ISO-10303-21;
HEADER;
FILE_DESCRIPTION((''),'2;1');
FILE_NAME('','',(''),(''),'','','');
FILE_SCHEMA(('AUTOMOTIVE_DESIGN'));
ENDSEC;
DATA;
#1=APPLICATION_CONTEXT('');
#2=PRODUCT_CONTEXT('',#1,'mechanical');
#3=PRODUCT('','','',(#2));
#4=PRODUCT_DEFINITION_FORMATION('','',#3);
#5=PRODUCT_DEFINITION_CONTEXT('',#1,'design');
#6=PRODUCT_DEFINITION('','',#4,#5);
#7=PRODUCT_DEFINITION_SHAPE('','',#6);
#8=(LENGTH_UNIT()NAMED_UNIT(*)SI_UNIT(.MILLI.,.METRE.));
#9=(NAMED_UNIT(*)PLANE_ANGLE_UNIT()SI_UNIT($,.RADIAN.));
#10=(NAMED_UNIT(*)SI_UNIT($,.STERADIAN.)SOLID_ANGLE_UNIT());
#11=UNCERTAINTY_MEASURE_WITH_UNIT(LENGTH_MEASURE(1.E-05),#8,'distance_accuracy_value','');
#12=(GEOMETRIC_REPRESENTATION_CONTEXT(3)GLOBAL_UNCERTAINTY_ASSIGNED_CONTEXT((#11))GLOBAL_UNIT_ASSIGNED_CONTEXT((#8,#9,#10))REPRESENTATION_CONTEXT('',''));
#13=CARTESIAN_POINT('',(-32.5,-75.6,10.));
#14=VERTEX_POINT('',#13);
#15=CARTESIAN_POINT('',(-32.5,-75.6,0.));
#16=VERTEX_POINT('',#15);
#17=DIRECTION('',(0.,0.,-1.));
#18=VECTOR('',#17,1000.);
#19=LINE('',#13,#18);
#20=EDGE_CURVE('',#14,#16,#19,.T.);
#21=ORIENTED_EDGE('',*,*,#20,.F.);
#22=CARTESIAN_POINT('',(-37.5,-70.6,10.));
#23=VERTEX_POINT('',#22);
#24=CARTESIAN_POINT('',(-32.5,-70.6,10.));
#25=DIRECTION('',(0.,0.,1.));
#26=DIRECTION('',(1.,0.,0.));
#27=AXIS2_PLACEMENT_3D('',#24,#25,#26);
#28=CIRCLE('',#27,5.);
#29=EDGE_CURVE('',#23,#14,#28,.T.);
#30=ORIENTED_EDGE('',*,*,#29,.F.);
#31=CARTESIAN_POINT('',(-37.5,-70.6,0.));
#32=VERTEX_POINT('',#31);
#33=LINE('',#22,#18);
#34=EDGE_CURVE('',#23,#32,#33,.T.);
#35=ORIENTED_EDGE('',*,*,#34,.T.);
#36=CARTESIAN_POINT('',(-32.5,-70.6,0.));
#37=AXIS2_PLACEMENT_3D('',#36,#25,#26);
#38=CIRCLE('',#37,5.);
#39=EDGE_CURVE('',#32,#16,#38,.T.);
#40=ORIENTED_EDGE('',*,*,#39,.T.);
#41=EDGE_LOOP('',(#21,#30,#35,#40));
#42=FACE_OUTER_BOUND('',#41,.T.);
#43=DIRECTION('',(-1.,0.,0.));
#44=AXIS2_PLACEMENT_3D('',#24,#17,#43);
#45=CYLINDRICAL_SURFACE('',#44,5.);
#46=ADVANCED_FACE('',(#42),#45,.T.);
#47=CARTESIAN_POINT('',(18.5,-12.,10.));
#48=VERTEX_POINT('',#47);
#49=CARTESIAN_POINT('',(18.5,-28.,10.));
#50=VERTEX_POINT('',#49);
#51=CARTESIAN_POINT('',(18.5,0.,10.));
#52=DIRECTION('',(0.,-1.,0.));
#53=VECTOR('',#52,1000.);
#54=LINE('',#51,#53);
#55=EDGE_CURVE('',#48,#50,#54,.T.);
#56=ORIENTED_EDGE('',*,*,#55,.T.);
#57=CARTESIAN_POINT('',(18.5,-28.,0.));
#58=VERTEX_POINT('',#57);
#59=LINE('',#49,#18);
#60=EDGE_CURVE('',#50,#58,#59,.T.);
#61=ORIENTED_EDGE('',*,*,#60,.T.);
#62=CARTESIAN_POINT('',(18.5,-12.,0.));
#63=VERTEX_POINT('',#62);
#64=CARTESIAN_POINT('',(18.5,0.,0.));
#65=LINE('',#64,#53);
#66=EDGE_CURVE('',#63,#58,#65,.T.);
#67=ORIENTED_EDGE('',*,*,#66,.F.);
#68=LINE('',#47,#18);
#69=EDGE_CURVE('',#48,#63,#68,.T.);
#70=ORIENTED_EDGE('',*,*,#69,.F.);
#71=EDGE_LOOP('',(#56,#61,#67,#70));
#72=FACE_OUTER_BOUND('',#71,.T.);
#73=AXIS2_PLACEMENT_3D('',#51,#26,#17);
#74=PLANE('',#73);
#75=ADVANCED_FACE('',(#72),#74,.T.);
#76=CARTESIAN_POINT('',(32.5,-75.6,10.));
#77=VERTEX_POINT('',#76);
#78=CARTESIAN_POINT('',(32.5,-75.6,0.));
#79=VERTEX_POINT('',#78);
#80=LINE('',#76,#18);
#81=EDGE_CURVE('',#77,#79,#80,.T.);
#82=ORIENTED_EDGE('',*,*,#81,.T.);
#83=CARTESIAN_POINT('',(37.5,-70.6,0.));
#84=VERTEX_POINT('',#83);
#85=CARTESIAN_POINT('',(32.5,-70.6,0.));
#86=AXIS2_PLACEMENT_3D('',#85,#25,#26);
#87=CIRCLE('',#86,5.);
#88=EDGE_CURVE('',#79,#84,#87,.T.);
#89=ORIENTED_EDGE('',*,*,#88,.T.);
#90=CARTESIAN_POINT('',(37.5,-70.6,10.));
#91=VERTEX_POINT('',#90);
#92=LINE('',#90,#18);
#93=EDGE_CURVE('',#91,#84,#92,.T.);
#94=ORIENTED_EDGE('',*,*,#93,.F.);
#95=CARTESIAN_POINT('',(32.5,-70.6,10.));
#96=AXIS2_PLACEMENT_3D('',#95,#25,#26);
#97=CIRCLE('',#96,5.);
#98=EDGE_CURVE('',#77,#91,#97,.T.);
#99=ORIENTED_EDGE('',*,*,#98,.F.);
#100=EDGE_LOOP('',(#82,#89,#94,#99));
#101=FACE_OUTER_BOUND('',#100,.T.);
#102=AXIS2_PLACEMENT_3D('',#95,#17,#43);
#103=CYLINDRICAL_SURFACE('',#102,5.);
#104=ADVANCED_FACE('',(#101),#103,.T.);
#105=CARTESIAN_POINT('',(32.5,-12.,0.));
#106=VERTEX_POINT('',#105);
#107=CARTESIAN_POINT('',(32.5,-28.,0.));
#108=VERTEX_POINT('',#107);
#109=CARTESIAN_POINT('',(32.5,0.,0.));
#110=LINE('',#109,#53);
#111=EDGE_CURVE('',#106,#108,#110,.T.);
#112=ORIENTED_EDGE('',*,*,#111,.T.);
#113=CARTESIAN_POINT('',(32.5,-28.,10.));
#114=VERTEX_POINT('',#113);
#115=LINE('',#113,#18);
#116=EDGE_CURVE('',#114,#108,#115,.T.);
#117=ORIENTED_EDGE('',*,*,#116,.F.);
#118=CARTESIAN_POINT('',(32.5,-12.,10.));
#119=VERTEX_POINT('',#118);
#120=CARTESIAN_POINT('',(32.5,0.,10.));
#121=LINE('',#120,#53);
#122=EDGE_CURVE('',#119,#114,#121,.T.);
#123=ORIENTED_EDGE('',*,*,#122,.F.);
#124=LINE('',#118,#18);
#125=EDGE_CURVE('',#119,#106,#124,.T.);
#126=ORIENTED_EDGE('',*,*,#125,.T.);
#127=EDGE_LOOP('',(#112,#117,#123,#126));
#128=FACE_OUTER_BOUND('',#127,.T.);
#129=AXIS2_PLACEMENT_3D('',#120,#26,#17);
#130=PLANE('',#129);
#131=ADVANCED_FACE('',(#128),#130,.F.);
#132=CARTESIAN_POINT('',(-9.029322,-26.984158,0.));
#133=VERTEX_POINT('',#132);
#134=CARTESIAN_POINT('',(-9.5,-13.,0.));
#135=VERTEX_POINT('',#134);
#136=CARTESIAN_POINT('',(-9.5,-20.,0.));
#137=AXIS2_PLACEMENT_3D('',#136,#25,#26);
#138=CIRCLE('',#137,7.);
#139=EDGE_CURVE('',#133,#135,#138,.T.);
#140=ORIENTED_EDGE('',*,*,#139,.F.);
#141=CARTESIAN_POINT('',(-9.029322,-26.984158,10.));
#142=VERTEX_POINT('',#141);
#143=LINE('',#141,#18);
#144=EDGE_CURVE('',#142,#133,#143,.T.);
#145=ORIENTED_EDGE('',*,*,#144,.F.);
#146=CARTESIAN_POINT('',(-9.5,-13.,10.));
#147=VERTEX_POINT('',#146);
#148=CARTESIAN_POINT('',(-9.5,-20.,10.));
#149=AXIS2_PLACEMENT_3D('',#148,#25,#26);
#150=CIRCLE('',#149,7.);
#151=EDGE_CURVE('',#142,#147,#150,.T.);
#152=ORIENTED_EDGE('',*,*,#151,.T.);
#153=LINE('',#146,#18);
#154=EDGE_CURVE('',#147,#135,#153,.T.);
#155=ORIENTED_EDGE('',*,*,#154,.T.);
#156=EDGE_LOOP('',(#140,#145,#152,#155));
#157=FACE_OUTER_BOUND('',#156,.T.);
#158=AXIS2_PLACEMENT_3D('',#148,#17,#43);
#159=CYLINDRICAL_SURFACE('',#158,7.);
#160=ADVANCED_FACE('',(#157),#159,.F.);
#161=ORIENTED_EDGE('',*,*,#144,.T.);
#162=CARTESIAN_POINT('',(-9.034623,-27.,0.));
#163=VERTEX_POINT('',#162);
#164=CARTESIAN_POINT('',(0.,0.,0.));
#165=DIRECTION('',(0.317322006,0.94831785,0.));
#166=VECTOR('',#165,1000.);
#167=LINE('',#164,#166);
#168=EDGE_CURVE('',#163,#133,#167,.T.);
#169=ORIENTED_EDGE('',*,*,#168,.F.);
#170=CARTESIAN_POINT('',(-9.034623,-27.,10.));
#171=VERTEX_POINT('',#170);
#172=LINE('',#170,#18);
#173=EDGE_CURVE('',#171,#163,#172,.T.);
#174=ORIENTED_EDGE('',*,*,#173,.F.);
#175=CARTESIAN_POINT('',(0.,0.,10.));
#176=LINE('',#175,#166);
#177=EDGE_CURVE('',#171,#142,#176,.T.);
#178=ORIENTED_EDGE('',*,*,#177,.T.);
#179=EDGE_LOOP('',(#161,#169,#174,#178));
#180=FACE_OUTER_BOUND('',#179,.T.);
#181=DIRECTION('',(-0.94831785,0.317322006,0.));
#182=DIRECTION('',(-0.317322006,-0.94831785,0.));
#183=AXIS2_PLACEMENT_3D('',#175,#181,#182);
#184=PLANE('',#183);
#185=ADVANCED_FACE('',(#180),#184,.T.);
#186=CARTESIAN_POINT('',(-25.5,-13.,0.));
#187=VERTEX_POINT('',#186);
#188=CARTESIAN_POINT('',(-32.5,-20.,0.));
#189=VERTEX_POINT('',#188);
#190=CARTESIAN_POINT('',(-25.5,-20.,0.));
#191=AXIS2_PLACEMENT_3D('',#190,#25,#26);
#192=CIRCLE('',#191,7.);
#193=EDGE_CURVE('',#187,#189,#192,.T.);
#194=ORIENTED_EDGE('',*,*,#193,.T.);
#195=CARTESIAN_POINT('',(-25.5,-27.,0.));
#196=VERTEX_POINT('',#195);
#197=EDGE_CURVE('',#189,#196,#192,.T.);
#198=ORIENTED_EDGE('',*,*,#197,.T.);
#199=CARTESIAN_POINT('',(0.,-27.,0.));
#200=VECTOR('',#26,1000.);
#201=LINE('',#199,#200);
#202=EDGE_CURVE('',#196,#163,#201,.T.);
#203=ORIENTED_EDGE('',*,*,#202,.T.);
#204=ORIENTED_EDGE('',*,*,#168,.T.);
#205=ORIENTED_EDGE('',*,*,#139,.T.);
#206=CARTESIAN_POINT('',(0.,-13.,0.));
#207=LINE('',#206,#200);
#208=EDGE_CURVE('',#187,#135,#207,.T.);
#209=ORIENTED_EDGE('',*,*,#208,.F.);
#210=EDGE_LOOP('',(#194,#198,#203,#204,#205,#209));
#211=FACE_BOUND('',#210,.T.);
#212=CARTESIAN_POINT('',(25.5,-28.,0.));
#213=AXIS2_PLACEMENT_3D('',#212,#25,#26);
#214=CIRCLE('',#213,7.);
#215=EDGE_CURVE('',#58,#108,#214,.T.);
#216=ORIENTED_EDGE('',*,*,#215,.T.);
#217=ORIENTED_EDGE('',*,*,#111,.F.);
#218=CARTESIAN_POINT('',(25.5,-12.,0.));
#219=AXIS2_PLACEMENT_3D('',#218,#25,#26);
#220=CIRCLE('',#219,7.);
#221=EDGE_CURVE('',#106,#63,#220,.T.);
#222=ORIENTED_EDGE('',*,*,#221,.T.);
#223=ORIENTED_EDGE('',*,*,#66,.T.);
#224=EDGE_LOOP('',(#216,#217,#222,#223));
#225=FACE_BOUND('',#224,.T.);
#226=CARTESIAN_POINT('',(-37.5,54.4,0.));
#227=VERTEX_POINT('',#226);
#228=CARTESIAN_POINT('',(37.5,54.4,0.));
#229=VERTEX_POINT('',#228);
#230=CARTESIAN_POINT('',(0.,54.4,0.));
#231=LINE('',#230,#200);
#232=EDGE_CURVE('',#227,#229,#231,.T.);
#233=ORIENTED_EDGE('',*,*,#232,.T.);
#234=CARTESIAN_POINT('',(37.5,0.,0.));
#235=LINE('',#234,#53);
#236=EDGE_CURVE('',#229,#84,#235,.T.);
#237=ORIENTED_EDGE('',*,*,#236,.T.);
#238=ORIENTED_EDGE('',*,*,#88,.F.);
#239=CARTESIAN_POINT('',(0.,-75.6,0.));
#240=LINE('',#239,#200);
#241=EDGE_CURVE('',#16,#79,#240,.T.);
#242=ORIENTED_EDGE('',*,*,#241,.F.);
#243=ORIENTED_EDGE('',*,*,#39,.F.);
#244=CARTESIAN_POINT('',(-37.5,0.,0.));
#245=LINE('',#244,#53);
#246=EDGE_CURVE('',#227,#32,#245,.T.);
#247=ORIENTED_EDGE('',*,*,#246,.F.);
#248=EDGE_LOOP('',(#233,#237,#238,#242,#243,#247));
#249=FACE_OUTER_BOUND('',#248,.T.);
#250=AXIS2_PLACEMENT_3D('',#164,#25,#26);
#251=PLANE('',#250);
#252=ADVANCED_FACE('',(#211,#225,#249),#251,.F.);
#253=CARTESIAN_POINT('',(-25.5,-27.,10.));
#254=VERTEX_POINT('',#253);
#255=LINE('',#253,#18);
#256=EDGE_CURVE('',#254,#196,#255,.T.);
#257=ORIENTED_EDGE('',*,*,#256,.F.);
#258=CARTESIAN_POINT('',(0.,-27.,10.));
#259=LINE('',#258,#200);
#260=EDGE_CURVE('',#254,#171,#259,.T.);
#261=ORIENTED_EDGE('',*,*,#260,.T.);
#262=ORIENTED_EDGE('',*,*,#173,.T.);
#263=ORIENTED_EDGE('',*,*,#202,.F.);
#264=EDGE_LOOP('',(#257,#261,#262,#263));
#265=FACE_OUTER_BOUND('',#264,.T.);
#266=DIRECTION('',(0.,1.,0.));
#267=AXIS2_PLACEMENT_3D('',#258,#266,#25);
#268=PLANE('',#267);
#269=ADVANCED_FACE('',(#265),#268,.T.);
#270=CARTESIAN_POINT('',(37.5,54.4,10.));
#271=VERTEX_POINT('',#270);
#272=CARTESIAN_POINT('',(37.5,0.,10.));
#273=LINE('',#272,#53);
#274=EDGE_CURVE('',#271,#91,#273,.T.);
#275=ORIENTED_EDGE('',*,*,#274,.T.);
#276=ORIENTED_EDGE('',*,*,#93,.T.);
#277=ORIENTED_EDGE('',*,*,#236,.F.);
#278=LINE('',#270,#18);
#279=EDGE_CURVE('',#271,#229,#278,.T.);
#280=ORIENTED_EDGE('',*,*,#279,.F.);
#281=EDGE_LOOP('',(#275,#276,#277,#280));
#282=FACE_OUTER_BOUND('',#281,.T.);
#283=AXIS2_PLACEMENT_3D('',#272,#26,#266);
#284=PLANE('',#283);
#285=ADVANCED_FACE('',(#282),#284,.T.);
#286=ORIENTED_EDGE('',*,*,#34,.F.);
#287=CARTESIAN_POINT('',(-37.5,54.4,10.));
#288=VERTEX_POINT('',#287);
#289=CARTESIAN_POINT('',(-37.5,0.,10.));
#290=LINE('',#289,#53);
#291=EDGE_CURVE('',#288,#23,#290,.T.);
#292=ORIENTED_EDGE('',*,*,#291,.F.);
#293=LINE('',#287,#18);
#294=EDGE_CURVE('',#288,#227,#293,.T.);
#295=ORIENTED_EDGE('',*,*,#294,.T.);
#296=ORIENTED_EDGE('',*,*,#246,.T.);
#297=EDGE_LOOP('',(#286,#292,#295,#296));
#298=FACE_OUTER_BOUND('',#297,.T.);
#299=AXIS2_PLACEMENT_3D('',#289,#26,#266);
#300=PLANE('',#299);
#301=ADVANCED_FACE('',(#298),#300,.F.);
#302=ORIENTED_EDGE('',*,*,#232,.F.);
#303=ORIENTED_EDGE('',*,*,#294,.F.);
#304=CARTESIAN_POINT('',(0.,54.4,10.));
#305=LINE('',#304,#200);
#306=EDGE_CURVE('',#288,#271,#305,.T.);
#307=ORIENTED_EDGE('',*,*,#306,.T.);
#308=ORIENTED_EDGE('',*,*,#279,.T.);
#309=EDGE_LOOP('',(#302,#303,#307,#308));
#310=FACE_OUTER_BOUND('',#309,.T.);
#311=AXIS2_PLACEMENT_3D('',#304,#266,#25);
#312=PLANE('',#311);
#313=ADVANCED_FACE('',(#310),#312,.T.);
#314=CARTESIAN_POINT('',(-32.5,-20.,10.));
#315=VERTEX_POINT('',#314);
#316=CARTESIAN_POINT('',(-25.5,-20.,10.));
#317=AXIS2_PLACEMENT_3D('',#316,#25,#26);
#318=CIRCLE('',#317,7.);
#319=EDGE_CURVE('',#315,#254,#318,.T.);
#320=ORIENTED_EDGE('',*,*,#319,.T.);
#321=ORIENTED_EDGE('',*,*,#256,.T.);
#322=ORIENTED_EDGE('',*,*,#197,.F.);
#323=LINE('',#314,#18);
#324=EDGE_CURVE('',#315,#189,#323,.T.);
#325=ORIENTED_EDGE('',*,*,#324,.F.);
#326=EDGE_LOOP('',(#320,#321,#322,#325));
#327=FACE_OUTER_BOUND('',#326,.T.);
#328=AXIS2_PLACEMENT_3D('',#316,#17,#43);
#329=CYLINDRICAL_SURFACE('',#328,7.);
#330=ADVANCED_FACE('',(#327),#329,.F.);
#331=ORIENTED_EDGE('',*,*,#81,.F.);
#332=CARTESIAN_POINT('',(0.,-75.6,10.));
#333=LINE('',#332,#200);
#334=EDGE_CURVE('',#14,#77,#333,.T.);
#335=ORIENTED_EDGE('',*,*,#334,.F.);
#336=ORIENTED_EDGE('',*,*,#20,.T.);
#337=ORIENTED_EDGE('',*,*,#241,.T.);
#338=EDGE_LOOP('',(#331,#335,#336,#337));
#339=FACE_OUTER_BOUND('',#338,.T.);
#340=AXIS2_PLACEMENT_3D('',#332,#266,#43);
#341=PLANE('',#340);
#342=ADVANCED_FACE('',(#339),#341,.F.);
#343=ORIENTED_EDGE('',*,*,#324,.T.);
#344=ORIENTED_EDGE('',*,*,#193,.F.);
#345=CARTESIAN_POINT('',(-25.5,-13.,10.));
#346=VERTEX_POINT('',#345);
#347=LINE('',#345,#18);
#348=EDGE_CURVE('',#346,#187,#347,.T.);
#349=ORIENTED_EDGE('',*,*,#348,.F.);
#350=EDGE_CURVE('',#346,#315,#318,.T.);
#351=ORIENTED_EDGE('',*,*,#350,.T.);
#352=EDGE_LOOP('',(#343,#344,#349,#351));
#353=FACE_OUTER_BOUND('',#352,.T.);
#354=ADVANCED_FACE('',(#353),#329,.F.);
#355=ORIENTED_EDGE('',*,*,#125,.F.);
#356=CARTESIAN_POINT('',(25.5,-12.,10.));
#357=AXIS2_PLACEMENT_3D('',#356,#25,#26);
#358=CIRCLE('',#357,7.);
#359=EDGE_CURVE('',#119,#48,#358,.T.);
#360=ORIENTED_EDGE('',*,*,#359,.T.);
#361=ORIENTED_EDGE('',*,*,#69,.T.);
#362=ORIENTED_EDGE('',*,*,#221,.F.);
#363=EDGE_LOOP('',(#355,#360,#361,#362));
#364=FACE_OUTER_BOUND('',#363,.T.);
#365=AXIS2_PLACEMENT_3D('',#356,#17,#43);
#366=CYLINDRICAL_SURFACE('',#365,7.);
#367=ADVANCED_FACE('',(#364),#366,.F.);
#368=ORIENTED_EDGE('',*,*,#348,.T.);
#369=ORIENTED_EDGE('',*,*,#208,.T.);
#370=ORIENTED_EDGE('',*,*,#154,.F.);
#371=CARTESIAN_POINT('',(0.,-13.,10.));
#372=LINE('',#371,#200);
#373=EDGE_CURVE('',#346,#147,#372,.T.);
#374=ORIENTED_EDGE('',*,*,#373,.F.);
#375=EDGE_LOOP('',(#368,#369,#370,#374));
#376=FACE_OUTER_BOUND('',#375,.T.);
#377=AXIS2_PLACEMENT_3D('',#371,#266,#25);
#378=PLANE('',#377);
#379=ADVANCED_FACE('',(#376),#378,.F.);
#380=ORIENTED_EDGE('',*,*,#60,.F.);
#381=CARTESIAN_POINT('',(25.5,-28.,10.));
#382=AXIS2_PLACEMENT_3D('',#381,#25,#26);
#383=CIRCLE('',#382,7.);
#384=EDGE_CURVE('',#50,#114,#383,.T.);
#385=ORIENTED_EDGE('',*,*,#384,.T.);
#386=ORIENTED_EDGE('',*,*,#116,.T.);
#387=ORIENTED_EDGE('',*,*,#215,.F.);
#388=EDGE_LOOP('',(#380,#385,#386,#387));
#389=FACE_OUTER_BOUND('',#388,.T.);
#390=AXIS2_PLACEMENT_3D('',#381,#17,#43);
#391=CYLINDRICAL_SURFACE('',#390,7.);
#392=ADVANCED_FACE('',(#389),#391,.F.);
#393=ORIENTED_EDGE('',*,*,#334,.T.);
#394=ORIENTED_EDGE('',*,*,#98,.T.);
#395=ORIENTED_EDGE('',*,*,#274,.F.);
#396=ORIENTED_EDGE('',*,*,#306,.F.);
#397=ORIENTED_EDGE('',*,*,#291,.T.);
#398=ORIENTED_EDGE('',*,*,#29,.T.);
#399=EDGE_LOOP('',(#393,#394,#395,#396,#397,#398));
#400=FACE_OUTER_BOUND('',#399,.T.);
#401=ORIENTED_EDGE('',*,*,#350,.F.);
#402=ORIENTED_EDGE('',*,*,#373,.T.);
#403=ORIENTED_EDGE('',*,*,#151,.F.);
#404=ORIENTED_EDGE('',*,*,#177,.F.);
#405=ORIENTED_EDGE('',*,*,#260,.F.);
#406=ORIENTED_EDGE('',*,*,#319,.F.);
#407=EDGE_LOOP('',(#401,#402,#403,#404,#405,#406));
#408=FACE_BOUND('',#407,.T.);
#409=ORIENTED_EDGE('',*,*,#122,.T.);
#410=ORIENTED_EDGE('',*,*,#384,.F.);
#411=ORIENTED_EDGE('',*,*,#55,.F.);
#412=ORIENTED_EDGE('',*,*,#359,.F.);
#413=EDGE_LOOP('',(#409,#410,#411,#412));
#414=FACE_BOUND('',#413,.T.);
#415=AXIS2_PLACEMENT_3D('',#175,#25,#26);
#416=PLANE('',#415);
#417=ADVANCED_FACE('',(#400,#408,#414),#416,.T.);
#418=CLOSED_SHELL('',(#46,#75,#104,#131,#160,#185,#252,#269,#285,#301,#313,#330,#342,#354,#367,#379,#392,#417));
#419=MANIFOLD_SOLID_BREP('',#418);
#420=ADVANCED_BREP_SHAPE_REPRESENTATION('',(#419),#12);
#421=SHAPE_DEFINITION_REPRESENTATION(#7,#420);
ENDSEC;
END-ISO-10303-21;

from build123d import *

# Parameters (mm, degrees)
EXTRUDE_1_DEPTH = 10


with BuildPart() as part:
    # 草图1 → 凸台-拉伸1 (new body)
    with BuildSketch(Plane.XY):
        with BuildLine():
            Line((-37.5, 54.4), (-37.5, -70.6))
            ThreePointArc((-37.5, -70.6), (-36.035533906, -74.135533906), (-32.5, -75.6))
            Line((-32.5, -75.6), (32.5, -75.6))
            ThreePointArc((32.5, -75.6), (36.035533906, -74.135533906), (37.5, -70.6))
            Line((37.5, -70.6), (37.5, 54.4))
            Line((37.5, 54.4), (-37.5, 54.4))
        make_face()
        with BuildLine():
            Line((-9.03462289, -27), (-9.029321888, -26.984157939))
            ThreePointArc((-9.029321888, -26.984157939), (-2.503961636, -19.764527679), (-9.5, -13))
            Line((-9.5, -13), (-25.5, -13))
            ThreePointArc((-25.5, -13), (-32.5, -20), (-25.5, -27))
            Line((-25.5, -27), (-9.03462289, -27))
        make_face(mode=Mode.SUBTRACT)
        with BuildLine():
            ThreePointArc((18.5, -28), (25.5, -35), (32.5, -28))
            Line((32.5, -28), (32.5, -12))
            ThreePointArc((32.5, -12), (25.5, -5), (18.5, -12))
            Line((18.5, -12), (18.5, -28))
        make_face(mode=Mode.SUBTRACT)
    extrude(amount=EXTRUDE_1_DEPTH)


solid = part.part
